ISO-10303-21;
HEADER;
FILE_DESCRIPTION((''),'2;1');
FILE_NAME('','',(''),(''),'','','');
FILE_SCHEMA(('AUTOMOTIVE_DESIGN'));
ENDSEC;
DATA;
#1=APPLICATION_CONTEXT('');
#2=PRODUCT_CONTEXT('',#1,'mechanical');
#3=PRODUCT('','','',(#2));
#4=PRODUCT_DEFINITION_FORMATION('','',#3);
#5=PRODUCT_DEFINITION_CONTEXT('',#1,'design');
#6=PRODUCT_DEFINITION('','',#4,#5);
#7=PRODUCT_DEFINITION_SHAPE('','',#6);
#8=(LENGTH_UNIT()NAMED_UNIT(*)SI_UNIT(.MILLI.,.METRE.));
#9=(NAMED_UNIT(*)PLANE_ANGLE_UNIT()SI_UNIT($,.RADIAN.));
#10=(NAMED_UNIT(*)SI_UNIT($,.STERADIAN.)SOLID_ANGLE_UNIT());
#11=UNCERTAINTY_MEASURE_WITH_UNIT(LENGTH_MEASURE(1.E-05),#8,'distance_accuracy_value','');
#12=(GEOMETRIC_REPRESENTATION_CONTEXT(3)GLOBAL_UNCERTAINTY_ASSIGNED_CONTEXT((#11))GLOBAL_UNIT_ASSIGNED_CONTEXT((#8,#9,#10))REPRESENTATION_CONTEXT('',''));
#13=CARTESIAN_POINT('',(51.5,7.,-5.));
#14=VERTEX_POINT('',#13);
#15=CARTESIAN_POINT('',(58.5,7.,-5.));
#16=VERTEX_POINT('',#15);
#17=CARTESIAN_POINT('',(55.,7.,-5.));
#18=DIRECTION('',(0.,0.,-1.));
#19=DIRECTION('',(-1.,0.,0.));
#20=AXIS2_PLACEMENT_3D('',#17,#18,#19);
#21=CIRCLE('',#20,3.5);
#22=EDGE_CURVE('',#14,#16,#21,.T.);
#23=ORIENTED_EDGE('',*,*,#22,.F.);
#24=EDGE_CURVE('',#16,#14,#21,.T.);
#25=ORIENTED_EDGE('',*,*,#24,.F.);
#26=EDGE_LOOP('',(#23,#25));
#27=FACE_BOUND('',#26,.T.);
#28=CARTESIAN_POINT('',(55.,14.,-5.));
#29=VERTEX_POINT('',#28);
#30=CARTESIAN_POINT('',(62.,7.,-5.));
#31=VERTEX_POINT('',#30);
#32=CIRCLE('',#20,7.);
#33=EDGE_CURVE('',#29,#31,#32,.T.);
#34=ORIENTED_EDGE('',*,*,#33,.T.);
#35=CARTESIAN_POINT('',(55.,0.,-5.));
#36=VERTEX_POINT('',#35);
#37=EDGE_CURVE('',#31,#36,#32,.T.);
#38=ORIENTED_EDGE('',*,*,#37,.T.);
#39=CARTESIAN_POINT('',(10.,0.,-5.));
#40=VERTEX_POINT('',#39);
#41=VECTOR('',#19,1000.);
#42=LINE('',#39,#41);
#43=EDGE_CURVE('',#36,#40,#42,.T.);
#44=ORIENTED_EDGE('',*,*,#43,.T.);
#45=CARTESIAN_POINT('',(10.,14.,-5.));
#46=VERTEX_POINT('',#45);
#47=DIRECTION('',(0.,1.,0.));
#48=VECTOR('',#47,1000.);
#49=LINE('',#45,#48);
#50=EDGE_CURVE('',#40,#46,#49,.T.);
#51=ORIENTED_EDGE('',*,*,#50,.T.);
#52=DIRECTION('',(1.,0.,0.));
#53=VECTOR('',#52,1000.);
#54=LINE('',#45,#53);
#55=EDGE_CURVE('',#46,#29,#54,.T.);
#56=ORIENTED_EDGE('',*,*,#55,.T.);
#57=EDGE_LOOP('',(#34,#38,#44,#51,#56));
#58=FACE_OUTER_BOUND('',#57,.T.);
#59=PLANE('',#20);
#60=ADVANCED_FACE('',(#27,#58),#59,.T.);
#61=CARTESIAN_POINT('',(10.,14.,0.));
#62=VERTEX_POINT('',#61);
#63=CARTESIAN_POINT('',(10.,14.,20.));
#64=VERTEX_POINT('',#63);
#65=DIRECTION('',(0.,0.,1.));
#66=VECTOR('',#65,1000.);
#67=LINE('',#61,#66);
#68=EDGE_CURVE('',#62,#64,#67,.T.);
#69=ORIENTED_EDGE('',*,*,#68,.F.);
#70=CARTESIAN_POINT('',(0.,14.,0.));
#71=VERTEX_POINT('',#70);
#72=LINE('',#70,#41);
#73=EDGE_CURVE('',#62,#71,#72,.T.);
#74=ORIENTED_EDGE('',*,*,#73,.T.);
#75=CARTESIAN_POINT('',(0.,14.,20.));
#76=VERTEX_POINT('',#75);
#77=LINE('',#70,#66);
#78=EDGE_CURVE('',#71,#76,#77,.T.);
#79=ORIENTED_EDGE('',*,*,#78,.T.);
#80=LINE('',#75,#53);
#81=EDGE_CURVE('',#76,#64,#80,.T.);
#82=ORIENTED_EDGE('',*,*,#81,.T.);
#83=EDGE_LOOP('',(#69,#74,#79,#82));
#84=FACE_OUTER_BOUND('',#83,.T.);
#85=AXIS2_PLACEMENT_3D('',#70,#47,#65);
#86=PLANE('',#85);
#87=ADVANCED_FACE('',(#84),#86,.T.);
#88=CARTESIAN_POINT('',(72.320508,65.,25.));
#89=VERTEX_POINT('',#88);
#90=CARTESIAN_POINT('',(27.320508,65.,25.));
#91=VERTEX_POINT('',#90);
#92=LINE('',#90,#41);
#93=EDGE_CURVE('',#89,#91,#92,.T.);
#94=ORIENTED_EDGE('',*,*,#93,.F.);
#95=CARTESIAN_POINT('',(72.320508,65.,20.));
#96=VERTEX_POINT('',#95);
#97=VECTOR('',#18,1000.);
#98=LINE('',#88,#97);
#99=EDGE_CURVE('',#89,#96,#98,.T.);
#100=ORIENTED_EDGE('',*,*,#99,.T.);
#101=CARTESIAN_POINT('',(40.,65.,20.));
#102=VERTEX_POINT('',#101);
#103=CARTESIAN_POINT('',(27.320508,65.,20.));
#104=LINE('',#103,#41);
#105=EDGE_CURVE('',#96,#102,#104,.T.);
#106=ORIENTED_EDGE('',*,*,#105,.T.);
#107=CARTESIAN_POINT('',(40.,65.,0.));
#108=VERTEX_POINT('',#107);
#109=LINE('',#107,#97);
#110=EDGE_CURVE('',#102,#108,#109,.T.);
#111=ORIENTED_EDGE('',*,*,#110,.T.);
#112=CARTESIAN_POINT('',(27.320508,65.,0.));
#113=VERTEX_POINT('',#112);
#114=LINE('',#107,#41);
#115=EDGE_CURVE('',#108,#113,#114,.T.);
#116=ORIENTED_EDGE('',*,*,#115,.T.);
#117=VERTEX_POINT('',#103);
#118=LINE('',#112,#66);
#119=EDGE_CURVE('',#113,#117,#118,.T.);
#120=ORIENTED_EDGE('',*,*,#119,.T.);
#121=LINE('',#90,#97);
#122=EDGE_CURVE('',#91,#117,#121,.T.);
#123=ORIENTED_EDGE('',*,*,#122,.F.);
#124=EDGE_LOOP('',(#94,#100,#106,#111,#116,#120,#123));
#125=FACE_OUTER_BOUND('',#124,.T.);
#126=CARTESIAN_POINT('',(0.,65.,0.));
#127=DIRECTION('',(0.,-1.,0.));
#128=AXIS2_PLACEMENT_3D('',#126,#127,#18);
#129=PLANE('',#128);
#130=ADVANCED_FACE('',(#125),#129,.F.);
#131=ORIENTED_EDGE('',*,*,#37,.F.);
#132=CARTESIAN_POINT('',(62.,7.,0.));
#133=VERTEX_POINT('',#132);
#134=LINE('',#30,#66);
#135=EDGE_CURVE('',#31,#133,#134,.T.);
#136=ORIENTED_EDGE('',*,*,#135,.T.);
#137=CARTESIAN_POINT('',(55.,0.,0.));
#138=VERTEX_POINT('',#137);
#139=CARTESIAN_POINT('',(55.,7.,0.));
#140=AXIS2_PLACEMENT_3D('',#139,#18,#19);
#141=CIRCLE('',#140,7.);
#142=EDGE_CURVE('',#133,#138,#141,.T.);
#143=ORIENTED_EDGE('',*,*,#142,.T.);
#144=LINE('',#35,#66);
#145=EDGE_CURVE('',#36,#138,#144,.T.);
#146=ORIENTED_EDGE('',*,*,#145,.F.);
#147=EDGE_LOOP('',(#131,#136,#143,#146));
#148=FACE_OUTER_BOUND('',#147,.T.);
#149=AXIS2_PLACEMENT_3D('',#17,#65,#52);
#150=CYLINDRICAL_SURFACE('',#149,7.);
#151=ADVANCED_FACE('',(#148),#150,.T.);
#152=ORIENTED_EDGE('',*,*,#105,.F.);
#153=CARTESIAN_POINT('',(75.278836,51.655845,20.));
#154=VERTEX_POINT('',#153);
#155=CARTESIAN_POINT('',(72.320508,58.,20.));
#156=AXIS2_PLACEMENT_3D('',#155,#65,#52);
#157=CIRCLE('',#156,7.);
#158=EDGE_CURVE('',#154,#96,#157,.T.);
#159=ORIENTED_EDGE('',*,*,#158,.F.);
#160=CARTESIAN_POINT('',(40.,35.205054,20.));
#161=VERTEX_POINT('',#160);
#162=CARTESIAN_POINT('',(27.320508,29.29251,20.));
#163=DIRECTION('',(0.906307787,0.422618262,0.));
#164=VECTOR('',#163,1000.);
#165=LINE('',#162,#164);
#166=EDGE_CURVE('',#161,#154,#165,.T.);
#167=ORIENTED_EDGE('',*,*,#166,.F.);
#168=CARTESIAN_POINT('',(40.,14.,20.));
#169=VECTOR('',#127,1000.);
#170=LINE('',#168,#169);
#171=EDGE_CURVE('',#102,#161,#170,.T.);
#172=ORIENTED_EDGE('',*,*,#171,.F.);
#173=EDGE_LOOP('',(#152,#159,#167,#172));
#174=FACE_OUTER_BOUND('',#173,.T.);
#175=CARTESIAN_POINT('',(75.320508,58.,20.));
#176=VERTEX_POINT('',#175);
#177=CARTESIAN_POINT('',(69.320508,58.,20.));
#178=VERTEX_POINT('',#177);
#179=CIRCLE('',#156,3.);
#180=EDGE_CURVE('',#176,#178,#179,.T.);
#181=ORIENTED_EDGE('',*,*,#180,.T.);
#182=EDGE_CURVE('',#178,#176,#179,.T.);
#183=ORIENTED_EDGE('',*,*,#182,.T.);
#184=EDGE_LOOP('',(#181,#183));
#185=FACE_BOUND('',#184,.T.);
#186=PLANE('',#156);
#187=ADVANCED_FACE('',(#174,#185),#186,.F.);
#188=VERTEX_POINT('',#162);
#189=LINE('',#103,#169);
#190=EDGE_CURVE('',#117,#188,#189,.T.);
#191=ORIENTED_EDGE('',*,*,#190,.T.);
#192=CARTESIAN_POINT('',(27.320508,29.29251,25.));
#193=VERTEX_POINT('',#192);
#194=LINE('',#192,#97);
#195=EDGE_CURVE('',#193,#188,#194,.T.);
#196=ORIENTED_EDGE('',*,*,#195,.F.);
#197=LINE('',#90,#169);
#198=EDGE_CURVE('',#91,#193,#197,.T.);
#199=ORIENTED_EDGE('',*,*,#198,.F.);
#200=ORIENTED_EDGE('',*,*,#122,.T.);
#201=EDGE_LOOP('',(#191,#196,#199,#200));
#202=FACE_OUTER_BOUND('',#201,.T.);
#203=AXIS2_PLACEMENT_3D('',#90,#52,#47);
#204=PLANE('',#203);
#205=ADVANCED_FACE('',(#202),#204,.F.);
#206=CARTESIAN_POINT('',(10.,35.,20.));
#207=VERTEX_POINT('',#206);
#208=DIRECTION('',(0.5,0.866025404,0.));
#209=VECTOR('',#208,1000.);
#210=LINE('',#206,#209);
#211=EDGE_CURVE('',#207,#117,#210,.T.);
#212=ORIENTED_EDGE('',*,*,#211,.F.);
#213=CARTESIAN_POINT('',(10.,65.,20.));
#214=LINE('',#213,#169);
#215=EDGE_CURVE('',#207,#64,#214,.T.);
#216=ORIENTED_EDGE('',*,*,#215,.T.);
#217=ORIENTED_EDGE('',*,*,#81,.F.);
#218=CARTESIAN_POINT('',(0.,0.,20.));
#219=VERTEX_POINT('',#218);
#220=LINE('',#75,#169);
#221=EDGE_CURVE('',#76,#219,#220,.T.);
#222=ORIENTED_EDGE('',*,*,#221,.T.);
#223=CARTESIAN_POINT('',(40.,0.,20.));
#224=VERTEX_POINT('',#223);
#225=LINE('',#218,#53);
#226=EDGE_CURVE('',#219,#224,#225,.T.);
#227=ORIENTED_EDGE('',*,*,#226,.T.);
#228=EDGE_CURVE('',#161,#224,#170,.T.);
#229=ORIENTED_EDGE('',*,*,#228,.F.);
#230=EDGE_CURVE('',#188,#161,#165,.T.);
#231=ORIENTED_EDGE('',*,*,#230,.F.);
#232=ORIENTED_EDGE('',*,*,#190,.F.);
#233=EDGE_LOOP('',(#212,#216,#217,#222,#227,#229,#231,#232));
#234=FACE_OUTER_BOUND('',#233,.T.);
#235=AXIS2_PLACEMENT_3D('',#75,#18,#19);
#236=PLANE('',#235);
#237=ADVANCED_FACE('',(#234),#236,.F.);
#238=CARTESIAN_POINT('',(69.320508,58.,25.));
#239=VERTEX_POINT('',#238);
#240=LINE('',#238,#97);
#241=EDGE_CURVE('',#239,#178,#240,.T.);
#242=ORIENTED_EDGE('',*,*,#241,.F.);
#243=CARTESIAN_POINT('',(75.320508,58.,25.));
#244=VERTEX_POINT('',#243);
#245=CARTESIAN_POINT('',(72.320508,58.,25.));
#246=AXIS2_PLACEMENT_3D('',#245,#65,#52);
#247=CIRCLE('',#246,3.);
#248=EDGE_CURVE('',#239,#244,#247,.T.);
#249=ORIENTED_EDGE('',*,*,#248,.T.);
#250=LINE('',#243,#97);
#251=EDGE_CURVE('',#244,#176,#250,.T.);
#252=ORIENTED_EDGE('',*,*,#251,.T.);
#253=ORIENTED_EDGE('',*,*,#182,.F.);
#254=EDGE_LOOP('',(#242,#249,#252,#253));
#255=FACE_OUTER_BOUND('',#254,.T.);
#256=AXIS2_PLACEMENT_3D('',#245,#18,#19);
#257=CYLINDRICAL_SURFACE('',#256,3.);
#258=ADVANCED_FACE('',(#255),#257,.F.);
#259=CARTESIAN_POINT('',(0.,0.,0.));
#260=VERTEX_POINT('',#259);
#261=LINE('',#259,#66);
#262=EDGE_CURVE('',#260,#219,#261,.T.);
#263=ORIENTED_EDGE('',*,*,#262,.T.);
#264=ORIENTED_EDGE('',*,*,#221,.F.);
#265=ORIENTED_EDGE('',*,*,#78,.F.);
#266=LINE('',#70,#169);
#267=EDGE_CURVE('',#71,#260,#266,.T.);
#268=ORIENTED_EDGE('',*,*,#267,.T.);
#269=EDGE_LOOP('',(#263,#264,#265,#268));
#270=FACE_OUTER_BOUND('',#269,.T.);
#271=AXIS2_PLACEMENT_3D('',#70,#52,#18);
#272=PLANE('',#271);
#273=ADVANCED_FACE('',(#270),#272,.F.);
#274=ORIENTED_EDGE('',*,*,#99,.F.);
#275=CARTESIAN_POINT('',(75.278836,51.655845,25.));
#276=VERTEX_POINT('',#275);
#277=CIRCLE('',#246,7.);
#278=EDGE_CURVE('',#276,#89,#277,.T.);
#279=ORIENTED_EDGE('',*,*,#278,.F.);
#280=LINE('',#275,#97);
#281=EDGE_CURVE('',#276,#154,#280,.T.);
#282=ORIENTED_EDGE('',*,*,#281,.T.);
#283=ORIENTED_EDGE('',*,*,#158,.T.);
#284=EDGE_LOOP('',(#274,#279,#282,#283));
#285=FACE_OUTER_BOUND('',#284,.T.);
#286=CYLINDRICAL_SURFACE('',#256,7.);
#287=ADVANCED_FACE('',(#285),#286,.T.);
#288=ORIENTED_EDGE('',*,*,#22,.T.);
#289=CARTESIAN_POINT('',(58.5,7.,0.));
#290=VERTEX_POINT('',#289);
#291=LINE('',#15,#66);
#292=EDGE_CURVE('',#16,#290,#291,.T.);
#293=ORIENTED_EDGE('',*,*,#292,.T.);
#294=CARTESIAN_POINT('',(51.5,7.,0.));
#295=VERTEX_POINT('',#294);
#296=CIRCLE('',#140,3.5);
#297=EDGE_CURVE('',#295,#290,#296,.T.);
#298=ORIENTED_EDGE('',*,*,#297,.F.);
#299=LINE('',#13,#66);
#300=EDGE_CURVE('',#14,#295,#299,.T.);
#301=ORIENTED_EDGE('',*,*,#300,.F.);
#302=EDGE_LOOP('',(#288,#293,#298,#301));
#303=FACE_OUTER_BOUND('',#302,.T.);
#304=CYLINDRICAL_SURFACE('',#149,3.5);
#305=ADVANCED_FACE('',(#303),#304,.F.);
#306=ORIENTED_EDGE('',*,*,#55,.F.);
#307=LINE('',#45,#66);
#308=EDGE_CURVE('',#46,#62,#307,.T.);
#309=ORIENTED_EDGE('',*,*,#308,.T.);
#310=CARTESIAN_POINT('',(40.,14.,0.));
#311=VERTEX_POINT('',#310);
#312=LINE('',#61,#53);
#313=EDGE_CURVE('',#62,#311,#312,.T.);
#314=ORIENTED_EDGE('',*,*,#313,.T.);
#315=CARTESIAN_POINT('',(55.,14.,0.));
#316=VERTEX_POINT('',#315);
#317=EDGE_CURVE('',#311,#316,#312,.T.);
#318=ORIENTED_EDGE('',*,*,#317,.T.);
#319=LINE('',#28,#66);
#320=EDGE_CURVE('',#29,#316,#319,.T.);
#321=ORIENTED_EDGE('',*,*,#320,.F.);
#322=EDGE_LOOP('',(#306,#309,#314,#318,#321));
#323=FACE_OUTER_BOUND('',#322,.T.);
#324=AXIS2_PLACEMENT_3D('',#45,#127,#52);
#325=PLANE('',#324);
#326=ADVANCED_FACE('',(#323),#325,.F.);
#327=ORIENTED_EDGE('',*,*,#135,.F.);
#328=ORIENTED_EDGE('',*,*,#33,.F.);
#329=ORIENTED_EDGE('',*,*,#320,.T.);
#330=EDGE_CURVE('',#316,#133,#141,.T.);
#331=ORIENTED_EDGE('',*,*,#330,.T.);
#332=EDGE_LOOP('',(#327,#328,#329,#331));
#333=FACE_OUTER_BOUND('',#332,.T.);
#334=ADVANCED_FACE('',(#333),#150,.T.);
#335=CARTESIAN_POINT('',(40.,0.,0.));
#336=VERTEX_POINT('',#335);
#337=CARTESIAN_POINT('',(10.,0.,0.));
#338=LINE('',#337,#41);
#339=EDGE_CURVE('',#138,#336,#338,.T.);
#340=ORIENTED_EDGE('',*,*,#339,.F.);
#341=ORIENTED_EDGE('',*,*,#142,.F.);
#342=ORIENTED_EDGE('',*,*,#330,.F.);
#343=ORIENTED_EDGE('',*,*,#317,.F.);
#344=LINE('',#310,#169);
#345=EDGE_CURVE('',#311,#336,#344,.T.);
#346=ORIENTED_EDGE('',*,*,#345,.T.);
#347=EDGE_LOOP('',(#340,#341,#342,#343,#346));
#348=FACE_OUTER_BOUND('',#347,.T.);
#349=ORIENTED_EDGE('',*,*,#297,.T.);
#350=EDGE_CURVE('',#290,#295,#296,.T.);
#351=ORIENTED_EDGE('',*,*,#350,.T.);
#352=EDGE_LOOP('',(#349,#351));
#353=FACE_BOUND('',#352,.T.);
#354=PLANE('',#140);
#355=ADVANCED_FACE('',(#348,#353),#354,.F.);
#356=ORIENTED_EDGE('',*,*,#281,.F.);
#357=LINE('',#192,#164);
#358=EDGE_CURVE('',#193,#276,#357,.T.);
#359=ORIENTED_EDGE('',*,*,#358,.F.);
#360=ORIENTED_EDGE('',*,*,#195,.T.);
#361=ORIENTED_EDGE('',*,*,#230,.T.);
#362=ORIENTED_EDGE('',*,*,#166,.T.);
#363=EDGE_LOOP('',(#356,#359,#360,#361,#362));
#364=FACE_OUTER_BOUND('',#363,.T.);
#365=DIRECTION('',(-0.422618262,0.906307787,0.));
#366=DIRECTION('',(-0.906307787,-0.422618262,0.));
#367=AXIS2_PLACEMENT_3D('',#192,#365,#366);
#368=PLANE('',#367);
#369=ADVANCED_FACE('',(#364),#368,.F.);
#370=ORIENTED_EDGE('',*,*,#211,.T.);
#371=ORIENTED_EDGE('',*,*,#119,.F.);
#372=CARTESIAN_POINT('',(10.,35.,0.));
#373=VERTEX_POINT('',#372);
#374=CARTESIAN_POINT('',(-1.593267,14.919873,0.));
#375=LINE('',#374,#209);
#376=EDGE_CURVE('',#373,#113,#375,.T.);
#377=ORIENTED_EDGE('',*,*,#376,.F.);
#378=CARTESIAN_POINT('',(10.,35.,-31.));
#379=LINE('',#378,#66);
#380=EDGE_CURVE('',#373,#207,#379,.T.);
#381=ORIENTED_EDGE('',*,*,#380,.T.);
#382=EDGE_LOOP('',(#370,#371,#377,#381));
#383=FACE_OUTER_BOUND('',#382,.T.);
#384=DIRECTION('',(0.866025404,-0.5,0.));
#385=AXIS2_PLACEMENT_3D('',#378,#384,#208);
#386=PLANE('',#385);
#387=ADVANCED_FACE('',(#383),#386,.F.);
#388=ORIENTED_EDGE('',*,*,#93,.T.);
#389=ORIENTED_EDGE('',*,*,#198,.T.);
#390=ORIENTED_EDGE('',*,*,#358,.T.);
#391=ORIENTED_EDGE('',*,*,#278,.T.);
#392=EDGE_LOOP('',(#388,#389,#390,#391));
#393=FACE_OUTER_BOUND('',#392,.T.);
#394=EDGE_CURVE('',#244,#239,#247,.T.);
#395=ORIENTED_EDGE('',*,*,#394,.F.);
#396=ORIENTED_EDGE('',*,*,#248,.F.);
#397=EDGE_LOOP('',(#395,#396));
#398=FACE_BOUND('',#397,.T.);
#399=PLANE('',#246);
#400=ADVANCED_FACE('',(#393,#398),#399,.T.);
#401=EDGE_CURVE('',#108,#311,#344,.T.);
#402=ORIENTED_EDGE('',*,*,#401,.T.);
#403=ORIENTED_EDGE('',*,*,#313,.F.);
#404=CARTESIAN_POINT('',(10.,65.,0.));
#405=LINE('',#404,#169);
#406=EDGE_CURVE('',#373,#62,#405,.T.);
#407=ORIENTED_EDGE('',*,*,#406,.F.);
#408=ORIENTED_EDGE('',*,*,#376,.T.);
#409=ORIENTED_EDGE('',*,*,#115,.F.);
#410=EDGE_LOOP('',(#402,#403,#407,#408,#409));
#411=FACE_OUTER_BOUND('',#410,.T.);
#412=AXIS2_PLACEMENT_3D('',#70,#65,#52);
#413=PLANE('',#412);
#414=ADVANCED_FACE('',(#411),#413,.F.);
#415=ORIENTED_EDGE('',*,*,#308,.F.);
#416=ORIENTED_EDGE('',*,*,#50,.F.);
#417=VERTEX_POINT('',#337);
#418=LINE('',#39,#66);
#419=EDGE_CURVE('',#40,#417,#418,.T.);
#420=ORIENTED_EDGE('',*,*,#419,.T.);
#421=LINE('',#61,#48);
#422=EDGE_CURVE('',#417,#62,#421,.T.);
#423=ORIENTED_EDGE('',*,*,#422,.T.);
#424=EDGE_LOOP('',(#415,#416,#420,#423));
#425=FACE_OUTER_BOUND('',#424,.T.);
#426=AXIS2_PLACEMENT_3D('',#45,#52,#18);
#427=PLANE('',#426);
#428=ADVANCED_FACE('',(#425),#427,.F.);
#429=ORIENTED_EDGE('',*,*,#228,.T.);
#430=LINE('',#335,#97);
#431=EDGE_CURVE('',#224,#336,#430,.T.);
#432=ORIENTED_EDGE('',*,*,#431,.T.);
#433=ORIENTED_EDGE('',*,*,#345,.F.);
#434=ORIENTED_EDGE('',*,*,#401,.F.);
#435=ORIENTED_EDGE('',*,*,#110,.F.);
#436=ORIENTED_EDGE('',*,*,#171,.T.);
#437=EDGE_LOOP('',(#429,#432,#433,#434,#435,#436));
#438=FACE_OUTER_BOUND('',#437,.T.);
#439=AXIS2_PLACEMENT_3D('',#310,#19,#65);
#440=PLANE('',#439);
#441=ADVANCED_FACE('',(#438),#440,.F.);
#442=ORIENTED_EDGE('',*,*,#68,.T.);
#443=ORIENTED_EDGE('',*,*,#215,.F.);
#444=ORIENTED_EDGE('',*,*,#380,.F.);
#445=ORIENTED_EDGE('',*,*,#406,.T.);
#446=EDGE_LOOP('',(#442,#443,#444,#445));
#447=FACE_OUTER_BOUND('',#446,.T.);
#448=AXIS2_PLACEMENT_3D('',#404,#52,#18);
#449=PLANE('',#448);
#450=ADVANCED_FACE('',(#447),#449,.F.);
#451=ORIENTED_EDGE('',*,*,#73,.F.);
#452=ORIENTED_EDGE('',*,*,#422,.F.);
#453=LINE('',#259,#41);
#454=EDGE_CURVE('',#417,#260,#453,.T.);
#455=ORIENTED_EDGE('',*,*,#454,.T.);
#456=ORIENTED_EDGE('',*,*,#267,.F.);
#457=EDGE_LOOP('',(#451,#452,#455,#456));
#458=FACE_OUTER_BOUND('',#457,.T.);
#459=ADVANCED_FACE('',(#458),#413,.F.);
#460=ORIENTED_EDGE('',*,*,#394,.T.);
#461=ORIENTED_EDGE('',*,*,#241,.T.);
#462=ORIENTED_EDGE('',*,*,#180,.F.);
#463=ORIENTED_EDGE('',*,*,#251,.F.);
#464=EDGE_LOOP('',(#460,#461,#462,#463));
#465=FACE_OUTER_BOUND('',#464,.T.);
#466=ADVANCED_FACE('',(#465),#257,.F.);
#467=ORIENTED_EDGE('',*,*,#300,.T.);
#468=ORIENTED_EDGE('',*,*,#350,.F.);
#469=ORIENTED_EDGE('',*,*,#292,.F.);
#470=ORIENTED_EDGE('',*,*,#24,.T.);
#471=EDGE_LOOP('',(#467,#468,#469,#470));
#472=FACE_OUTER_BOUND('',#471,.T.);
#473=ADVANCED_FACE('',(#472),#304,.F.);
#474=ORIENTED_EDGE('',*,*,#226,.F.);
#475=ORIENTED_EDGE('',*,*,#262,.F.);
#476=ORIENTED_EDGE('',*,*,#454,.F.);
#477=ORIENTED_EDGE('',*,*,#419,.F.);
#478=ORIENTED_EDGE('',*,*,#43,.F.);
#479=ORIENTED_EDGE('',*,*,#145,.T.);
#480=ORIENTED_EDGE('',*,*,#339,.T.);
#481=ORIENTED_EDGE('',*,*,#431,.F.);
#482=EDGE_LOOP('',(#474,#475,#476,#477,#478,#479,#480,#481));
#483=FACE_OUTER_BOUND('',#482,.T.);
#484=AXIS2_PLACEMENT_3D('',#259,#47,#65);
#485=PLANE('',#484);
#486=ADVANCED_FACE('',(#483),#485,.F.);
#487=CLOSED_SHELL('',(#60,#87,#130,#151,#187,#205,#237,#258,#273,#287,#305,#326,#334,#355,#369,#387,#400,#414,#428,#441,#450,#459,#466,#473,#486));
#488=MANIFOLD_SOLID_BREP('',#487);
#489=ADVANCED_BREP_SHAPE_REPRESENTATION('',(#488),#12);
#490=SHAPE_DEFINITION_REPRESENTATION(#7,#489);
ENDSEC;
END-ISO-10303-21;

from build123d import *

# Parameters (mm, degrees)
BASE_BLOCK_SKETCH_W    = 40
BASE_BLOCK_SKETCH_H    = 20
BASE_BLOCK_DEPTH       = 14
UPRIGHT_SKETCH_W       = 30
UPRIGHT_SKETCH_H       = 20
UPRIGHT_BLOCK_DEPTH    = 51
ANGLED_CUT_30DEG_DEPTH = 51
UPPER_LUG_SKETCH_R     = 3
UPPER_LUG_DEPTH        = 5
LOWER_LUG_SKETCH_R     = 3.5
LOWER_LUG_DEPTH        = 5


with BuildPart() as part:
    # Base Block Sketch → Base Block (new body)
    with BuildSketch(Plane(origin=(0, 0, 0), x_dir=(1, 0, 0), z_dir=(0, 1, 0))):
        with Locations((20, -10)):
            Rectangle(BASE_BLOCK_SKETCH_W, BASE_BLOCK_SKETCH_H)
    extrude(amount=BASE_BLOCK_DEPTH)

    # Upright Sketch → Upright Block (add)
    with BuildSketch(Plane(origin=(0, 14, 0), x_dir=(1, 0, 0), z_dir=(0, 1, 0))):
        with Locations((25, -10)):
            Rectangle(UPRIGHT_SKETCH_W, UPRIGHT_SKETCH_H)
    extrude(amount=UPRIGHT_BLOCK_DEPTH)

    # Angled Cut Sketch 30deg → Angled Cut 30deg (cut)
    with BuildSketch(Plane.XY.offset(20)):
        Polygon((10, 65), (10, 35), (27.320508076, 65), align=None)
    extrude(amount=-ANGLED_CUT_30DEG_DEPTH, mode=Mode.SUBTRACT)

    # Upper Lug Sketch → Upper Lug (add)
    with BuildSketch(Plane.XY.offset(20)):
        with BuildLine():
            Line((27.320508076, 65), (27.320508076, 29.29250995))
            Line((27.320508076, 29.29250995), (75.278835908, 51.655845491))
            ThreePointArc((75.278835908, 51.655845491), (79.154580126, 59.515077298), (72.320508076, 65))
            Line((72.320508076, 65), (27.320508076, 65))
        make_face()
        with Locations((72.320508076, 58)):
            Circle(UPPER_LUG_SKETCH_R, mode=Mode.SUBTRACT)
    extrude(amount=UPPER_LUG_DEPTH)

    # Lower Lug Sketch → Lower Lug (add)
    with BuildSketch(Plane(origin=(0, 0, 0), x_dir=(-1, 0, 0), z_dir=(0, 0, -1))):
        with BuildLine():
            Line((-10, 14), (-55, 14))
            ThreePointArc((-55, 14), (-62, 7), (-55, 0))
            Line((-55, 0), (-10, 0))
            Line((-10, 0), (-10, 14))
        make_face()
        with Locations((-55, 7)):
            Circle(LOWER_LUG_SKETCH_R, mode=Mode.SUBTRACT)
    extrude(amount=LOWER_LUG_DEPTH)


solid = part.part
